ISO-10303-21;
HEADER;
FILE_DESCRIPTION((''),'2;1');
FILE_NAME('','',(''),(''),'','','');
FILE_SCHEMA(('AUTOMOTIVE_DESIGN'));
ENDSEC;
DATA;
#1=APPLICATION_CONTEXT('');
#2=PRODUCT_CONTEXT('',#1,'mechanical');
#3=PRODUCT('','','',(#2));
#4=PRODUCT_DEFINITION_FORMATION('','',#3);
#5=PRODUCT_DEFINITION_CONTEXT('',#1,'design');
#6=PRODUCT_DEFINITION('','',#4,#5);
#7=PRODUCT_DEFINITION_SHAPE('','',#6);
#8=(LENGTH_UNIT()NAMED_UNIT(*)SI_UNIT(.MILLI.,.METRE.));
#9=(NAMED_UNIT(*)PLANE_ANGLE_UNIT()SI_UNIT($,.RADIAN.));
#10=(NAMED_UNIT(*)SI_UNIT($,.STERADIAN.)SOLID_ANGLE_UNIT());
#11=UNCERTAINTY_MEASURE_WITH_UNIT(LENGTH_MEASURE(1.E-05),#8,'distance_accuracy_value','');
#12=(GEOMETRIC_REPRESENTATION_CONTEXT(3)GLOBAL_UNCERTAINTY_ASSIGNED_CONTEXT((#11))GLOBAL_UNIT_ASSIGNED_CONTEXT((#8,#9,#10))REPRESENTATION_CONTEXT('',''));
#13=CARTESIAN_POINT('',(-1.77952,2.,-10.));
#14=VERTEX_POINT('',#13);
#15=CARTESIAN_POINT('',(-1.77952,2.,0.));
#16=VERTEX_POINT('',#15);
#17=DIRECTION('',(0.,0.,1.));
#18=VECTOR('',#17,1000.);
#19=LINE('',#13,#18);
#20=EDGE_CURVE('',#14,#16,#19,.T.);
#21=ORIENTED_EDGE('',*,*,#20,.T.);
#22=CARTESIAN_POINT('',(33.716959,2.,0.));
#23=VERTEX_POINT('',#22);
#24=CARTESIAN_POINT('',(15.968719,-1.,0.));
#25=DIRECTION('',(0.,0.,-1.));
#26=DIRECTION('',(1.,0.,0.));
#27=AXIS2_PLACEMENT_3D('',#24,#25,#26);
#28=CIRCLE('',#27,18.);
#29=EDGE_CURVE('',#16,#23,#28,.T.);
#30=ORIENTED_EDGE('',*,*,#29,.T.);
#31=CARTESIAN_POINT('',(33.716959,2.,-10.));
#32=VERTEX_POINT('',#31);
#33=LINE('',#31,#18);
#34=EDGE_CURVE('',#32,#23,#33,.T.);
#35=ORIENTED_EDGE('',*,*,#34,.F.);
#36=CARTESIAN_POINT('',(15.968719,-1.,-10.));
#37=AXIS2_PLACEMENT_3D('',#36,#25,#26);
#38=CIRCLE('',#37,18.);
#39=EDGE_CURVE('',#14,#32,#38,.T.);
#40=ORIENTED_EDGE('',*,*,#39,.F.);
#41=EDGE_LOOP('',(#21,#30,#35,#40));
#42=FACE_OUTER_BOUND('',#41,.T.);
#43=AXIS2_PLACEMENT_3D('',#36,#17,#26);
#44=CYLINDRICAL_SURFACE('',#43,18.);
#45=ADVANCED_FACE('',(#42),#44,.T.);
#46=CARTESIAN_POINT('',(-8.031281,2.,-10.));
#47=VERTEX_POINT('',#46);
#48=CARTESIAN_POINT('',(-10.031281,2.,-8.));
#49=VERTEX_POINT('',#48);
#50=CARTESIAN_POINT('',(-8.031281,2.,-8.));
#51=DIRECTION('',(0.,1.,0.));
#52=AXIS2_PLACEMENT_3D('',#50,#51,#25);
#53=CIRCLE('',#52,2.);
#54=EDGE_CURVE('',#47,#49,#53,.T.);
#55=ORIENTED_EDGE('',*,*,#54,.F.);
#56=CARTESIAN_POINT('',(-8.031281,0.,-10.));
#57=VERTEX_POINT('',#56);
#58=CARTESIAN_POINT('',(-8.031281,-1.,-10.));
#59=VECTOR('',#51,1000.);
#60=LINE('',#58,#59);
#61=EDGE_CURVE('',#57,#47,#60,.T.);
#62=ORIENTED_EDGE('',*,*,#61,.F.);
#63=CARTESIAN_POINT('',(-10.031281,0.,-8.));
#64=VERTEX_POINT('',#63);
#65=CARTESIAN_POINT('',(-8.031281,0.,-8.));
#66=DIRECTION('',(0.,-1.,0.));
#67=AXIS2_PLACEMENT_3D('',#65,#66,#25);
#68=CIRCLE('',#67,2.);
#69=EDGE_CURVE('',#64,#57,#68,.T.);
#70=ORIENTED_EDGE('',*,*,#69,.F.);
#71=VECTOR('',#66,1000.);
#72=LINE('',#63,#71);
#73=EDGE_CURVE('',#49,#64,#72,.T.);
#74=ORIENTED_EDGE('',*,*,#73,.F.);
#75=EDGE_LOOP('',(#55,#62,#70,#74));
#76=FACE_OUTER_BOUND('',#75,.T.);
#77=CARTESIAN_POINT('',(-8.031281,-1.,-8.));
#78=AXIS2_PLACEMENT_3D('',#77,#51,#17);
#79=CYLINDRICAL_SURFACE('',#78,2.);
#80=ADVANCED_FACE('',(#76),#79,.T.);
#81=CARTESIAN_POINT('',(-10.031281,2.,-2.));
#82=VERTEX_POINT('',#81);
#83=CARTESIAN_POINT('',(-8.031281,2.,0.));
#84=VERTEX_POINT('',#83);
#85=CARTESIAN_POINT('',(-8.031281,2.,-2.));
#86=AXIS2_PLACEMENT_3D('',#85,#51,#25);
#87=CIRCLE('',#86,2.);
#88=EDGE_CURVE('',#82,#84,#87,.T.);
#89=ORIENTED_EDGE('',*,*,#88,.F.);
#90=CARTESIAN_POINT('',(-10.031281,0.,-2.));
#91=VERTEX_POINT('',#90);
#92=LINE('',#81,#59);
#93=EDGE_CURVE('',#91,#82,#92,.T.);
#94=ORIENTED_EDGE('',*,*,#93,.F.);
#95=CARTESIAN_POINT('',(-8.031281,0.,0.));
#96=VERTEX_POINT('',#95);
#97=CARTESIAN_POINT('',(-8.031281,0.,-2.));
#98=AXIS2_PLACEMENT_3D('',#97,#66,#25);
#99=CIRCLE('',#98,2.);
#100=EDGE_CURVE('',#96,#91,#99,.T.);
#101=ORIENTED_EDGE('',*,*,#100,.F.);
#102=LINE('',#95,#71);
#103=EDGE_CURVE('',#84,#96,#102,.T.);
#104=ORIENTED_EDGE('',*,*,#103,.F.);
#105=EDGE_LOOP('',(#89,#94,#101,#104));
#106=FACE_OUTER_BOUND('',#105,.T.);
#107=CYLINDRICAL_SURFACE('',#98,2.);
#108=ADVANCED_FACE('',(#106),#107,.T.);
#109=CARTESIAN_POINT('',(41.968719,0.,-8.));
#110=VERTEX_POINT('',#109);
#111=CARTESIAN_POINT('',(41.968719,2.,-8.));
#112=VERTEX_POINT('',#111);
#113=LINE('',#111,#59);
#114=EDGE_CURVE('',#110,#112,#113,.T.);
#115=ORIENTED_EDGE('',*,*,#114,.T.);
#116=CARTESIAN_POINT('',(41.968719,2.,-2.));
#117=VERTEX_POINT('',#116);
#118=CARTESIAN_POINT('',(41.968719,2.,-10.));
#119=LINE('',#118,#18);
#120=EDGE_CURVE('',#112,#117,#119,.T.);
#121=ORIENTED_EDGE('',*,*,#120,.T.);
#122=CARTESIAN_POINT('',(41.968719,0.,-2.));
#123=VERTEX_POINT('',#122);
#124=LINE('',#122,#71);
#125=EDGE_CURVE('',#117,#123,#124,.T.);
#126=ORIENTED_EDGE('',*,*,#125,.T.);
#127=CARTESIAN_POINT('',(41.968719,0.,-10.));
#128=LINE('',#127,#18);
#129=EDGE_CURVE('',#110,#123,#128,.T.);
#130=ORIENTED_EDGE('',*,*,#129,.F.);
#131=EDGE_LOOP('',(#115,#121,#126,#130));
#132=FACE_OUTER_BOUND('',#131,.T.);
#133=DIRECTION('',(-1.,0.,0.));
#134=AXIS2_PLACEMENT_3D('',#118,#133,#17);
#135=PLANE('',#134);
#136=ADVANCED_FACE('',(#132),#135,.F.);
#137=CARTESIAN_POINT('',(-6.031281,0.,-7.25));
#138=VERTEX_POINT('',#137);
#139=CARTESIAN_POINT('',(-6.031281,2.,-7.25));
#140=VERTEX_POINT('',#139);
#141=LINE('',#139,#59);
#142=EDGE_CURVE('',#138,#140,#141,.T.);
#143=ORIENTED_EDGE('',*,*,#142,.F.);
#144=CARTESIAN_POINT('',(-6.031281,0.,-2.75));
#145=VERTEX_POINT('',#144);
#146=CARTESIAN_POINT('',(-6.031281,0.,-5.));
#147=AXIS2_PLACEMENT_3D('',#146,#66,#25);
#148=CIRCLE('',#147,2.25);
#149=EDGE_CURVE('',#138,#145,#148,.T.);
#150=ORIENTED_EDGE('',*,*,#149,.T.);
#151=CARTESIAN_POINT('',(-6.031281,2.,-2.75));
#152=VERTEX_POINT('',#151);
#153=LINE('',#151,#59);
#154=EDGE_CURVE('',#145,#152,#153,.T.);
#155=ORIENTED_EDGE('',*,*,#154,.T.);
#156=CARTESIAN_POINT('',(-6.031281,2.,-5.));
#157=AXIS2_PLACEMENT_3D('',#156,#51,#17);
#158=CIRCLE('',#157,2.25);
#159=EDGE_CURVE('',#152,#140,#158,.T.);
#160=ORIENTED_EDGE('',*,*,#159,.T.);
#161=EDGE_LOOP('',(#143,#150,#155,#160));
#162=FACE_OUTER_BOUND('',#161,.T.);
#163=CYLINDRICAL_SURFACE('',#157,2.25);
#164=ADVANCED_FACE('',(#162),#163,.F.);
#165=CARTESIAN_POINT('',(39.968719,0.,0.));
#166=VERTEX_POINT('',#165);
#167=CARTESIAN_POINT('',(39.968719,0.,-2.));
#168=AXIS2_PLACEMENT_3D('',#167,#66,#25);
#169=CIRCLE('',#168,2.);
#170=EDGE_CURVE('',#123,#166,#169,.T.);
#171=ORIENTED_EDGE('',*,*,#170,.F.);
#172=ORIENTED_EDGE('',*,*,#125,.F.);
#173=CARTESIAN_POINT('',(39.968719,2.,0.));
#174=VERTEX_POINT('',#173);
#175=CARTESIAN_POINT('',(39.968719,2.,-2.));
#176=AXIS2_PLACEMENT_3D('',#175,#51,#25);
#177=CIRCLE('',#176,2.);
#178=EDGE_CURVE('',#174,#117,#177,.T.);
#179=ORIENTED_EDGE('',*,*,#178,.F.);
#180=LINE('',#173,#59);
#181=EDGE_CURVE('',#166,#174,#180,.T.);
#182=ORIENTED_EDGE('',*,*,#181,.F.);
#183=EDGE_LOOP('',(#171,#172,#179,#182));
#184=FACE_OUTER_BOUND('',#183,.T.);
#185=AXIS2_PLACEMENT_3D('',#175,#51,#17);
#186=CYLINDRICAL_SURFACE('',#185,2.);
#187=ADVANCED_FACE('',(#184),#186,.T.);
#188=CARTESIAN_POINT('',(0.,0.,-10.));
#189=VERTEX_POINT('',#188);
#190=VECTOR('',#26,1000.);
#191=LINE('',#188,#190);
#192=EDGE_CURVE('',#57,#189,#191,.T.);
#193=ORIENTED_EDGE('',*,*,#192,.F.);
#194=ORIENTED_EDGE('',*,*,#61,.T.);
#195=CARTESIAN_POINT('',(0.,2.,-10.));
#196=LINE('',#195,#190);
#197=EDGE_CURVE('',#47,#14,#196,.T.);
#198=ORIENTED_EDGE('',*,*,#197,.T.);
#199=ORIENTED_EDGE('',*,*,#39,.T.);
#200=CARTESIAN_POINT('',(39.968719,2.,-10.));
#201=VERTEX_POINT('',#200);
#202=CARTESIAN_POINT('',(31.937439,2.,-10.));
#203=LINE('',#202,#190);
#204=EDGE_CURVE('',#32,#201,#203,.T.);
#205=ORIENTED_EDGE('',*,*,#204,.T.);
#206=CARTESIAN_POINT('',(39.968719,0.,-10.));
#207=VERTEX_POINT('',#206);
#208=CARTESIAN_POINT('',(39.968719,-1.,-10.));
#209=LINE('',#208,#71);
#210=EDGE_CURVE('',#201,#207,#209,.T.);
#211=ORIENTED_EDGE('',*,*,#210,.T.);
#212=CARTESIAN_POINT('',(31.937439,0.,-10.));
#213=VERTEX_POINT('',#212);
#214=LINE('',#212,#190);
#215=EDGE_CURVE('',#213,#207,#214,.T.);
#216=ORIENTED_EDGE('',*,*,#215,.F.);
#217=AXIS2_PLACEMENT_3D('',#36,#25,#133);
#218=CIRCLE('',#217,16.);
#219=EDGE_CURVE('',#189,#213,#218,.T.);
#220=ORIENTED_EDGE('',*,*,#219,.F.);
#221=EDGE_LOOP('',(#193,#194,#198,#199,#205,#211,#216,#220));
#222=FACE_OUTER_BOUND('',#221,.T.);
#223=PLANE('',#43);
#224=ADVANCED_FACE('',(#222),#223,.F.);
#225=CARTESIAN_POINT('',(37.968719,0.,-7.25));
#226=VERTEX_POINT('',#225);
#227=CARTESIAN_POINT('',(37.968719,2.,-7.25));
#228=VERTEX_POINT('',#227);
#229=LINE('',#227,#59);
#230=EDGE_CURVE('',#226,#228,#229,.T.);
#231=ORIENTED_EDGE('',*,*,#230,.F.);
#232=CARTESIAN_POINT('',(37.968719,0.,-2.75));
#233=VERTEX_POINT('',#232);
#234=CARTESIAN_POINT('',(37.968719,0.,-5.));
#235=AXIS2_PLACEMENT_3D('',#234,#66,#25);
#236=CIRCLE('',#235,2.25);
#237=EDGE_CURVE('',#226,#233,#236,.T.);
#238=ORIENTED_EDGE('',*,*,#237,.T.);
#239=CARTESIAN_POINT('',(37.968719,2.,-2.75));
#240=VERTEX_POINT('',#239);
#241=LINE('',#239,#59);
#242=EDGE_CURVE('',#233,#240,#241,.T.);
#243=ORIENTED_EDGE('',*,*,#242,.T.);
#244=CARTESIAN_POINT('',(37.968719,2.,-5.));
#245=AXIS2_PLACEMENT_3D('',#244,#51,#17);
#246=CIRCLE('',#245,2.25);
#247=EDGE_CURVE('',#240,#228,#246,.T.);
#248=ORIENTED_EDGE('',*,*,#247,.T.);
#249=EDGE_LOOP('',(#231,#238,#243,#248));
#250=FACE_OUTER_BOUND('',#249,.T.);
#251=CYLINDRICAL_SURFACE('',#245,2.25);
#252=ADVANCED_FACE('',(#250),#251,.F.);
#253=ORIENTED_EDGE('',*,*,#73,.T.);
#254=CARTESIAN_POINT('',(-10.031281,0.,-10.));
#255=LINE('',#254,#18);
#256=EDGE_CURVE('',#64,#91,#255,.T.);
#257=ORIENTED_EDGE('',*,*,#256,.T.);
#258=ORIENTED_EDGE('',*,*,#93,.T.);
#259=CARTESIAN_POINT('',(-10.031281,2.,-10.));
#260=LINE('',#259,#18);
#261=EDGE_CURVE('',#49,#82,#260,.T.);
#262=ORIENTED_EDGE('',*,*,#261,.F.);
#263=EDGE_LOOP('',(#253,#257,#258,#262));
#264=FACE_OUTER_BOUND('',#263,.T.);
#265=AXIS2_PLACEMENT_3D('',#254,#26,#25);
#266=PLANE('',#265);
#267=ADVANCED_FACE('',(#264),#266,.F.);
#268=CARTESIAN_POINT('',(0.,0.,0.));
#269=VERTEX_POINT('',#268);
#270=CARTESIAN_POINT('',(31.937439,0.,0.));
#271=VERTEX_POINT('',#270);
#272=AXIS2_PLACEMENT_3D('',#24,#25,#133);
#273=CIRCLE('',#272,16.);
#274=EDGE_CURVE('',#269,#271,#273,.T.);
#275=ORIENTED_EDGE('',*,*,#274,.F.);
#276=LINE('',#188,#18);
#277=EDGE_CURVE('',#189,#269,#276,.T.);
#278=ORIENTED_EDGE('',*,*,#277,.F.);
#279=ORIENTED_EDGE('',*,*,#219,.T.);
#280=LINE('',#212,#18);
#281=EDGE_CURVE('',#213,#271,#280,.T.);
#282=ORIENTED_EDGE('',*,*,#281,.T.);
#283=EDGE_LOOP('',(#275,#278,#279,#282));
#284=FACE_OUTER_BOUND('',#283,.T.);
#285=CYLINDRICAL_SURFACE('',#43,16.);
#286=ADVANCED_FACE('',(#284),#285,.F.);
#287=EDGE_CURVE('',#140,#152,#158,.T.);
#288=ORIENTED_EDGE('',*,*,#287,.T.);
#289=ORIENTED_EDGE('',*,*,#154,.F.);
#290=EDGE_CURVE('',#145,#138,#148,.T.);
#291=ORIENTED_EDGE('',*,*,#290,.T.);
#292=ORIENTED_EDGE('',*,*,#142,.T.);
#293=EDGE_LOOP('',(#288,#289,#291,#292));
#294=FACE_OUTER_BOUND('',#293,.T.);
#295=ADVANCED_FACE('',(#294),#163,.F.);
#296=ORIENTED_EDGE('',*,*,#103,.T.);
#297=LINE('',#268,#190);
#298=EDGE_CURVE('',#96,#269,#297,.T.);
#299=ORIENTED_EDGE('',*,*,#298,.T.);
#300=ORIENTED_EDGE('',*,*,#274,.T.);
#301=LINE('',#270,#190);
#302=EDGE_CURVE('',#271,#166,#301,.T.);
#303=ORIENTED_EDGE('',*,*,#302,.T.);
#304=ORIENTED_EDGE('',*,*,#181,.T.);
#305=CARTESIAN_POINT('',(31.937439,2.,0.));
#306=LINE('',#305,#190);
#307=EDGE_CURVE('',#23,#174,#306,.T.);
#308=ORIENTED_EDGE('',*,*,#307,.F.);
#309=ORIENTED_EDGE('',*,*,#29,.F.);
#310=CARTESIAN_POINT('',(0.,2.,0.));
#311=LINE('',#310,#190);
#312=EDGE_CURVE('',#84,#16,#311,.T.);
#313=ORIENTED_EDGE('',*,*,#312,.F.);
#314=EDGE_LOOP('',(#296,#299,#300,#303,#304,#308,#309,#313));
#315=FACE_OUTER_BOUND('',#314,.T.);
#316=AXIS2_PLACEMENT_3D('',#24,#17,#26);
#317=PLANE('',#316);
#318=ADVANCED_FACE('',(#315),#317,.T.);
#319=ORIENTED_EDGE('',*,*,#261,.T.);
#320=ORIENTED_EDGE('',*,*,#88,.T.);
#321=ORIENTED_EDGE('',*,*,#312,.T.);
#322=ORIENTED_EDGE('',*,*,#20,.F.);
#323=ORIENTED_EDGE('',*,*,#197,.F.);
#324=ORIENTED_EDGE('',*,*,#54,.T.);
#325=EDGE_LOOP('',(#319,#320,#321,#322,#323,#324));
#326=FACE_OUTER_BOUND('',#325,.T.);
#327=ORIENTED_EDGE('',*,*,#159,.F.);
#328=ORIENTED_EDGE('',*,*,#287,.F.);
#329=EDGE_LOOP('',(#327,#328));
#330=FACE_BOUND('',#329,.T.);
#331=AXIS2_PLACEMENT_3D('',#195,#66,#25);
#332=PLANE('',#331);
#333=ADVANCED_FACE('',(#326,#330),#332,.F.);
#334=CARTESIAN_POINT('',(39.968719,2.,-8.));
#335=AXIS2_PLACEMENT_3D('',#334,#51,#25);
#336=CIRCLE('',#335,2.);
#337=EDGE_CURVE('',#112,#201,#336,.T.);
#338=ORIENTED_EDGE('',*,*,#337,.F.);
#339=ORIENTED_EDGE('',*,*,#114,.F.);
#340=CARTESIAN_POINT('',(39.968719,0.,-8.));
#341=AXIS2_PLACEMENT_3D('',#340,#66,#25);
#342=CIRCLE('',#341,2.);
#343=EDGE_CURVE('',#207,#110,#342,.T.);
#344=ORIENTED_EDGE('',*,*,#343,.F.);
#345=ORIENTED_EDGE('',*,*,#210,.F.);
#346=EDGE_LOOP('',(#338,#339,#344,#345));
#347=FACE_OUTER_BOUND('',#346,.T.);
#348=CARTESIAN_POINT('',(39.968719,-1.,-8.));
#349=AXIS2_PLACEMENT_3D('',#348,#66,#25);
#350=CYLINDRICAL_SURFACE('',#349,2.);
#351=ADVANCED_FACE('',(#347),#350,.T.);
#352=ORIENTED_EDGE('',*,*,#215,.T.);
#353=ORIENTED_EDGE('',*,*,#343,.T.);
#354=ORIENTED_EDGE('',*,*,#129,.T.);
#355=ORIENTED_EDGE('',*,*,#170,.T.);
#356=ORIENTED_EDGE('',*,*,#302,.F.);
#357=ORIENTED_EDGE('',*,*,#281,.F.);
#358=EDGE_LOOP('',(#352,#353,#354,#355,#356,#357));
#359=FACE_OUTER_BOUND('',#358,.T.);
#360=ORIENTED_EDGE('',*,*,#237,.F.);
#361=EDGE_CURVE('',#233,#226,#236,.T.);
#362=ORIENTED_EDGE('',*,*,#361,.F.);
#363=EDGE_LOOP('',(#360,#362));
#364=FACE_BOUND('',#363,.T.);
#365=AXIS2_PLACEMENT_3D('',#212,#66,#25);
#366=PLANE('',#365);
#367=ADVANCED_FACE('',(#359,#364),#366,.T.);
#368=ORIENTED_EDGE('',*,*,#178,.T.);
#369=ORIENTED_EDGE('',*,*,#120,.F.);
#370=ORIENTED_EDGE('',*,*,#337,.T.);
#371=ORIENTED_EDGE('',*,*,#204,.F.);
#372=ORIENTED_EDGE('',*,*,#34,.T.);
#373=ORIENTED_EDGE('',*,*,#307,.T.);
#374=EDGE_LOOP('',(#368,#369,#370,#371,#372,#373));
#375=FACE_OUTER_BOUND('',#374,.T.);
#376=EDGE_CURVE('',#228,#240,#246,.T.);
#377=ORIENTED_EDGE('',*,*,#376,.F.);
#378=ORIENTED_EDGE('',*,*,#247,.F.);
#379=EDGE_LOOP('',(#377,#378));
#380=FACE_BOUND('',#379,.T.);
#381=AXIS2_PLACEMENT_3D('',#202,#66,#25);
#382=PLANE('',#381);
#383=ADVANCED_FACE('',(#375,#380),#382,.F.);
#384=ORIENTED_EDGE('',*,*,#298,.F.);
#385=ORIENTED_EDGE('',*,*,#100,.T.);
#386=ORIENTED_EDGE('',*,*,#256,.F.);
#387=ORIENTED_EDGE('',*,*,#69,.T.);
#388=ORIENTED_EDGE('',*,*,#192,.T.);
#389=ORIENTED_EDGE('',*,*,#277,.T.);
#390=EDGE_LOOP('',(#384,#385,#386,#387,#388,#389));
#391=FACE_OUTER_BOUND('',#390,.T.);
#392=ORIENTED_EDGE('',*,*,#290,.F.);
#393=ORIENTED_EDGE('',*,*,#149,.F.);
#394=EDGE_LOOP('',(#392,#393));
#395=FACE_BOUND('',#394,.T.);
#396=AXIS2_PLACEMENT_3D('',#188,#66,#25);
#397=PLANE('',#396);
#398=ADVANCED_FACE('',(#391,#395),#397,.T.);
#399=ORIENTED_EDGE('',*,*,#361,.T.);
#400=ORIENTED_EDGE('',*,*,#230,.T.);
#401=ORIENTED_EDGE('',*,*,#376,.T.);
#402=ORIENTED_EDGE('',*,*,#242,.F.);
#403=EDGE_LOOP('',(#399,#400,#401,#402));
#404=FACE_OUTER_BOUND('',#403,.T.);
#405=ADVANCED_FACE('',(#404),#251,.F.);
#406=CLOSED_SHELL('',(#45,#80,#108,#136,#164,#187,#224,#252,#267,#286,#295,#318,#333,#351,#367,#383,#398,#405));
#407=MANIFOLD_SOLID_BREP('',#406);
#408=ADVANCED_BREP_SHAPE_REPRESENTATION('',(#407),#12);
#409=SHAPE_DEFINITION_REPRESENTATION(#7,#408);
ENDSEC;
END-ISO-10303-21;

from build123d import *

# Parameters (mm, degrees)
EXTRUDE_THIN1_DEPTH      = 10
M4_CLEARANCE_HOLE1_D     = 4.5
M4_CLEARANCE_HOLE1_DEPTH = 124.5
M4_CLEARANCE_HOLE1_TIP   = 1.351936393
FILLET1_R                = 2


with BuildPart() as part:
    # Sketch1 → Extrude-Thin1 (new body)
    with BuildSketch(Plane.XY):
        with BuildLine():
            Line((41.968719423, 0), (31.937438845, 0))
            ThreePointArc((31.937438845, 0), (15.968719423, 15), (0, 0))
            Line((0, 0), (-10.031280577, 0))
            Line((-10.031280577, 0), (-10.031280577, 2))
            Line((-10.031280577, 2), (-1.779519927, 2))
            ThreePointArc((-1.779519927, 2), (15.968719423, 17), (33.716958772, 2))
            Line((33.716958772, 2), (41.968719423, 2))
            Line((41.968719423, 2), (41.968719423, 0))
        make_face()
    extrude(amount=-EXTRUDE_THIN1_DEPTH)

    # M4 Clearance Hole1
    with Locations(Plane(origin=(0, 2, 0), x_dir=(1, 0, 0), z_dir=(0, 1, 0))):
        with Locations((-6.031280577, 5), (37.968719423, 5)):
            Hole(M4_CLEARANCE_HOLE1_D / 2, depth=M4_CLEARANCE_HOLE1_DEPTH)
            with Locations((0, 0, -(M4_CLEARANCE_HOLE1_DEPTH + M4_CLEARANCE_HOLE1_TIP / 2))):  # 118° drill point
                Cone(0, M4_CLEARANCE_HOLE1_D / 2, M4_CLEARANCE_HOLE1_TIP, mode=Mode.SUBTRACT)

    # Fillet1
    fillet1_edges = [part.edges().sort_by_distance(p)[0] for p in [
        (-10.031280577, 1, -10),
        (41.968719423, 1, -10),
        (-10.031280577, 1, 0),
        (41.968719423, 1, 0),
    ]]
    fillet(fillet1_edges, radius=FILLET1_R)


solid = part.part
